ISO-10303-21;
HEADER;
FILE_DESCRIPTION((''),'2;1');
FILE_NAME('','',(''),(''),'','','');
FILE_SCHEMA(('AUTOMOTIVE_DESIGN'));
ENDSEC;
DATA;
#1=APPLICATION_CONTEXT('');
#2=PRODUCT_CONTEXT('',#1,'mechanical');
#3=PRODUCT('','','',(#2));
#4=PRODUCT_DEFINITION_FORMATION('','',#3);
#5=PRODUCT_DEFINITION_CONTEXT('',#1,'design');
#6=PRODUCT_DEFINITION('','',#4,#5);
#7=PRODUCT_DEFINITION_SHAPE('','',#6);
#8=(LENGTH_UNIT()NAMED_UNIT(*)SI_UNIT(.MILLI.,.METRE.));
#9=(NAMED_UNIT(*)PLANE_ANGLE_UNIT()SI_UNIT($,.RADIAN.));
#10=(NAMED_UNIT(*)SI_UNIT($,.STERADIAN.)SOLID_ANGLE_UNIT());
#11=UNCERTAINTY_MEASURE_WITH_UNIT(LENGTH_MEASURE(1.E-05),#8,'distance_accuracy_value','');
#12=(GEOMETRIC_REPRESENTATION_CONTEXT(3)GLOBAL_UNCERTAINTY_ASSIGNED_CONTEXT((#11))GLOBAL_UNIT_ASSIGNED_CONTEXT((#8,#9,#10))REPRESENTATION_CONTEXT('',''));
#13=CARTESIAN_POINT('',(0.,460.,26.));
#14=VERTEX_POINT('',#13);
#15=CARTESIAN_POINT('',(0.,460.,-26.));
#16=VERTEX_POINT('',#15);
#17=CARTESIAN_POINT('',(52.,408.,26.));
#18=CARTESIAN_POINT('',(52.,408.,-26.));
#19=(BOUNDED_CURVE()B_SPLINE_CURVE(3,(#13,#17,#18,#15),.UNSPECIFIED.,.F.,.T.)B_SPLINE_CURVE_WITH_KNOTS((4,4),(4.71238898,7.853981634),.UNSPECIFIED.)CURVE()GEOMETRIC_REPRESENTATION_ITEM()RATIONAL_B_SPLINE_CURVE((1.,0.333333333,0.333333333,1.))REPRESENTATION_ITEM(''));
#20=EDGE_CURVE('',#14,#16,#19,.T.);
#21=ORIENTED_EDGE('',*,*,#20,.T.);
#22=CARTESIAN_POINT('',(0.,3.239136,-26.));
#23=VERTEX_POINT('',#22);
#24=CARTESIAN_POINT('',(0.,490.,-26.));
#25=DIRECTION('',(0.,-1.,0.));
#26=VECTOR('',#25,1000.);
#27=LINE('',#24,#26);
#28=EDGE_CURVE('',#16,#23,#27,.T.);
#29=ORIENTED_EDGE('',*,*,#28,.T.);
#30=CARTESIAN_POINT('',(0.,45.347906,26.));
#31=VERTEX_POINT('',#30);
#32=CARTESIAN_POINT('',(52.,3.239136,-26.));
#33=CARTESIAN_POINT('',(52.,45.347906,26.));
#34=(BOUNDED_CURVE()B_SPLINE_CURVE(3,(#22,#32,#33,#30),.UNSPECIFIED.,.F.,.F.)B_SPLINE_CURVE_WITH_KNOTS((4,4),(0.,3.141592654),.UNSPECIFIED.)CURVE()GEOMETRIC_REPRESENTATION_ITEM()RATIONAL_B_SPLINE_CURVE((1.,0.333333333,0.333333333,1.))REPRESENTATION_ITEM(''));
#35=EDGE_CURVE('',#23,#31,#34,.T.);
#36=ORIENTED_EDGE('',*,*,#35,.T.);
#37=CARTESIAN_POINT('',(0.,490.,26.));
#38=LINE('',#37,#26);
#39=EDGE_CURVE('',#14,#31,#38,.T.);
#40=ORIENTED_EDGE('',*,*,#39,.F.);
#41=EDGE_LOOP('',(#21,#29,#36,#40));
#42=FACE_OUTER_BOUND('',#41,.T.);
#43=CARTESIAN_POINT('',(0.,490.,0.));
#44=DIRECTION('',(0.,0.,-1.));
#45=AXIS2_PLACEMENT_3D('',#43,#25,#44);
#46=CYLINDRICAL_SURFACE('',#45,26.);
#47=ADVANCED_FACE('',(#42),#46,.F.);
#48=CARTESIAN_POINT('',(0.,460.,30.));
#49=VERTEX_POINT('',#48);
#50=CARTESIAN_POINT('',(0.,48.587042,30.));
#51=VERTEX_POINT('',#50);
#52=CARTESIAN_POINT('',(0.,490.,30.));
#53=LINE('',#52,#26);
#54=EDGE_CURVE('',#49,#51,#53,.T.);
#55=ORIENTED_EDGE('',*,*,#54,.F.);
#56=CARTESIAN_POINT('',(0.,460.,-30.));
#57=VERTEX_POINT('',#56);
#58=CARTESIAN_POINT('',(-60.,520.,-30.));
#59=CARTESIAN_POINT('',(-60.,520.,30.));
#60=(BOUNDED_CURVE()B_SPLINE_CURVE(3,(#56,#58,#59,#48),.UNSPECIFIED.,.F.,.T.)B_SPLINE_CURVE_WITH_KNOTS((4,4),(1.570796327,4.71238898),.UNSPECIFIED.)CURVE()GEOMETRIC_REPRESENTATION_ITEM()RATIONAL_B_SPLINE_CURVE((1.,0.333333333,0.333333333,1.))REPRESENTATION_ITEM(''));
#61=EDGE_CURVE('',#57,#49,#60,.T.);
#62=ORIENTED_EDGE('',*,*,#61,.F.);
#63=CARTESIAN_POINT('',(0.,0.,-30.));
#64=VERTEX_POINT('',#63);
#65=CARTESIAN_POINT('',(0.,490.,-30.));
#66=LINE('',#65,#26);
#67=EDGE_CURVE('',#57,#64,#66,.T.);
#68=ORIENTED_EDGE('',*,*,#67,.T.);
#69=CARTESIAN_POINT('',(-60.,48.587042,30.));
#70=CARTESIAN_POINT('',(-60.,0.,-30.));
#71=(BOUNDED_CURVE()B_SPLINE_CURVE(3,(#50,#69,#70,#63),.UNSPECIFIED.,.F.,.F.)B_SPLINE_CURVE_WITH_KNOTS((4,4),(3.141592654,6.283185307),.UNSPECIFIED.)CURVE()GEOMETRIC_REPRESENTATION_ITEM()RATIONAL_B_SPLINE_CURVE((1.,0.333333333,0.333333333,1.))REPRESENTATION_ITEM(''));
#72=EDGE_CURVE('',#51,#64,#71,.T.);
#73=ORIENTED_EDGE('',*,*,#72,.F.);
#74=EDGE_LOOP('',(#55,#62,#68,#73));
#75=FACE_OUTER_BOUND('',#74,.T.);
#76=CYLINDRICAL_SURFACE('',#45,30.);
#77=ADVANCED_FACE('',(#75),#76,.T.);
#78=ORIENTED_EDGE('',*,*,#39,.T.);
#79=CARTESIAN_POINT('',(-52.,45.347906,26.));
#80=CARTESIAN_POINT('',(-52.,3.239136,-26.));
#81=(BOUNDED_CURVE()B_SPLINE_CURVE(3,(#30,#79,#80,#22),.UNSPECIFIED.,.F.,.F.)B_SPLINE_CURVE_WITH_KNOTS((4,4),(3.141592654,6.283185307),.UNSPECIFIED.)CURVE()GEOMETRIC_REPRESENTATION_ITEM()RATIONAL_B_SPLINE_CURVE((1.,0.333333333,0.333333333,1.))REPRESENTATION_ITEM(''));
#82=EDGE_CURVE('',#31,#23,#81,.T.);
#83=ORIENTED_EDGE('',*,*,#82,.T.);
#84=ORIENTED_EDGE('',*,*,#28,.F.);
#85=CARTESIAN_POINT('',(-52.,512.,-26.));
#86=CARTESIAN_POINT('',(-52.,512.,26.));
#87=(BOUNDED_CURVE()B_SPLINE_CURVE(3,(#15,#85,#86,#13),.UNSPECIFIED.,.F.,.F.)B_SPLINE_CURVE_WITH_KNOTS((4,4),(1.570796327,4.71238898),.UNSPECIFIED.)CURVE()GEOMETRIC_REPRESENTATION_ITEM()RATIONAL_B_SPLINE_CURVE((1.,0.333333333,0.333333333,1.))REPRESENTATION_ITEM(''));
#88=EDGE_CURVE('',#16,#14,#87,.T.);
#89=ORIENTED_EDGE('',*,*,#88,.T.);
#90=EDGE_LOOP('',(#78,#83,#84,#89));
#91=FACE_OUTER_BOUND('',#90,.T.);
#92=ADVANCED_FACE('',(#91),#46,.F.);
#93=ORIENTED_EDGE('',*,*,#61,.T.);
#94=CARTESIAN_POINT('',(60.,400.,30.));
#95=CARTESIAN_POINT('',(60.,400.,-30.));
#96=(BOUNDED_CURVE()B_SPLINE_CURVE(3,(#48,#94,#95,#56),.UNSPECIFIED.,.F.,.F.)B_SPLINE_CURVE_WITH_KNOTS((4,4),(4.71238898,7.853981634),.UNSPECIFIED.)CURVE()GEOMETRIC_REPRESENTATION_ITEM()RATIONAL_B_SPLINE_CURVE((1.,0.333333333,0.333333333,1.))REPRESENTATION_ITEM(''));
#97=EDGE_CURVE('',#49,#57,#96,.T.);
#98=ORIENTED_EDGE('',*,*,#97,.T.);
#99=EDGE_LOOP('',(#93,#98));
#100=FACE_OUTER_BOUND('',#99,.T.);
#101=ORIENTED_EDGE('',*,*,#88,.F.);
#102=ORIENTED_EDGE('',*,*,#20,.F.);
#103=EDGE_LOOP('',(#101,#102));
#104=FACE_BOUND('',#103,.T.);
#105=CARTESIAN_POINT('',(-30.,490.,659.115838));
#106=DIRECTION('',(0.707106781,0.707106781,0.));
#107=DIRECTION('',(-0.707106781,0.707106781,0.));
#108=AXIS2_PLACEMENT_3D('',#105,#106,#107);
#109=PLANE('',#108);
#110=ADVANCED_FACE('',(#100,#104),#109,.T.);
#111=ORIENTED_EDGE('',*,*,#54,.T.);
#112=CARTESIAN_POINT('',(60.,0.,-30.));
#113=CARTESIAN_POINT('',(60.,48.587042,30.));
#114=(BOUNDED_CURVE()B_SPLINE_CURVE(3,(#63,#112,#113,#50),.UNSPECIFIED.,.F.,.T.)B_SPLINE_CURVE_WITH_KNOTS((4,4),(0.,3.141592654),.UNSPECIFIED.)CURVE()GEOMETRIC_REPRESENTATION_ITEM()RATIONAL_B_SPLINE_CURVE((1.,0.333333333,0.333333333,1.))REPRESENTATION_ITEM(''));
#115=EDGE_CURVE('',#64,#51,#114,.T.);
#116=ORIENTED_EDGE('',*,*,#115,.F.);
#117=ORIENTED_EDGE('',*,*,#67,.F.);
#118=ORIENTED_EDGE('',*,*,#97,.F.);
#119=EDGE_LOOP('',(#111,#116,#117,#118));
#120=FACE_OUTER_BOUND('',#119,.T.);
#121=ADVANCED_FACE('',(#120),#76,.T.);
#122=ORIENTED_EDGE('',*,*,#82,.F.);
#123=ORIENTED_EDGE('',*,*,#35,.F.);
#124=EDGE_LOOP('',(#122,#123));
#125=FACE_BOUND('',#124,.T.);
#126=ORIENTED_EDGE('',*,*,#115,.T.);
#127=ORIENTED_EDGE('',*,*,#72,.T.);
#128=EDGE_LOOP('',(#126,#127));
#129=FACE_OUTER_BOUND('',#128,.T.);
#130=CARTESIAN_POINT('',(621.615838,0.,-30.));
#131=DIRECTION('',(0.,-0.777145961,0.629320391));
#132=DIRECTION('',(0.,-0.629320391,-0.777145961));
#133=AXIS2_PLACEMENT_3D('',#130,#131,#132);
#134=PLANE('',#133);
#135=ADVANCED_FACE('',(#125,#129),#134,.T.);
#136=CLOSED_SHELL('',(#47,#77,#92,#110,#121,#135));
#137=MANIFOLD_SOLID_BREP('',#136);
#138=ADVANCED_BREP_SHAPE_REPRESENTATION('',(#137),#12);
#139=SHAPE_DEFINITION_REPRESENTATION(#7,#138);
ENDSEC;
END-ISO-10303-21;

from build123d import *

# Parameters (mm, degrees)
SKETCH1_R               = 30
SKETCH1_R_2             = 26
BOSS_EXTRUDE1_DEPTH     = 490
CUT_EXTRUDE1_DEPTH      = 492.833305094
CUT_EXTRUDE1_DEPTH_BACK = 492.833305094
CUT_EXTRUDE2_DEPTH      = 492.833305094
CUT_EXTRUDE2_DEPTH_BACK = 492.833305094


with BuildPart() as part:
    # Sketch1 → Boss-Extrude1 (new body)
    with BuildSketch(Plane(origin=(0, 0, 0), x_dir=(1, 0, 0), z_dir=(0, 1, 0))):
        with Locations(Location((0, 0, 0), (0, 0, 270))):
            Circle(SKETCH1_R)
        with Locations(Location((0, 0, 0), (0, 0, 270))):
            Circle(SKETCH1_R_2, mode=Mode.SUBTRACT)
    extrude(amount=BOSS_EXTRUDE1_DEPTH)

    # Sketch2 → Cut-Extrude1 (cut, two sides: drawn at the far end of the back side and taken through both)
    with BuildSketch(Plane.XY.offset(-CUT_EXTRUDE1_DEPTH_BACK)):
        Polygon((-735.21145484, 1195.21145484), (-30, 490), (243.212319076, 216.787680924), (948.423773916, -488.423773916), (2358.846683596, 921.999135764), (675.21145484, 2605.63436452), align=None)
    extrude(amount=CUT_EXTRUDE1_DEPTH + CUT_EXTRUDE1_DEPTH_BACK, mode=Mode.SUBTRACT)

    # Sketch3 → Cut-Extrude2 (cut, two sides: drawn at the far end of the back side and taken through both)
    with BuildSketch(Plane(origin=(0, 0, 0), x_dir=(0, 0, -1), z_dir=(1, 0, 0)).offset(-CUT_EXTRUDE2_DEPTH_BACK)):
        Polygon((805.062902356, -627.63356305), (30, 0), (-69.882630866, 80.883359669), (-844.945533223, 708.516922719), (-2100.212659322, -841.608881993), (-450.204223743, -2177.759367762), align=None)
    extrude(amount=CUT_EXTRUDE2_DEPTH + CUT_EXTRUDE2_DEPTH_BACK, mode=Mode.SUBTRACT)


solid = part.part
